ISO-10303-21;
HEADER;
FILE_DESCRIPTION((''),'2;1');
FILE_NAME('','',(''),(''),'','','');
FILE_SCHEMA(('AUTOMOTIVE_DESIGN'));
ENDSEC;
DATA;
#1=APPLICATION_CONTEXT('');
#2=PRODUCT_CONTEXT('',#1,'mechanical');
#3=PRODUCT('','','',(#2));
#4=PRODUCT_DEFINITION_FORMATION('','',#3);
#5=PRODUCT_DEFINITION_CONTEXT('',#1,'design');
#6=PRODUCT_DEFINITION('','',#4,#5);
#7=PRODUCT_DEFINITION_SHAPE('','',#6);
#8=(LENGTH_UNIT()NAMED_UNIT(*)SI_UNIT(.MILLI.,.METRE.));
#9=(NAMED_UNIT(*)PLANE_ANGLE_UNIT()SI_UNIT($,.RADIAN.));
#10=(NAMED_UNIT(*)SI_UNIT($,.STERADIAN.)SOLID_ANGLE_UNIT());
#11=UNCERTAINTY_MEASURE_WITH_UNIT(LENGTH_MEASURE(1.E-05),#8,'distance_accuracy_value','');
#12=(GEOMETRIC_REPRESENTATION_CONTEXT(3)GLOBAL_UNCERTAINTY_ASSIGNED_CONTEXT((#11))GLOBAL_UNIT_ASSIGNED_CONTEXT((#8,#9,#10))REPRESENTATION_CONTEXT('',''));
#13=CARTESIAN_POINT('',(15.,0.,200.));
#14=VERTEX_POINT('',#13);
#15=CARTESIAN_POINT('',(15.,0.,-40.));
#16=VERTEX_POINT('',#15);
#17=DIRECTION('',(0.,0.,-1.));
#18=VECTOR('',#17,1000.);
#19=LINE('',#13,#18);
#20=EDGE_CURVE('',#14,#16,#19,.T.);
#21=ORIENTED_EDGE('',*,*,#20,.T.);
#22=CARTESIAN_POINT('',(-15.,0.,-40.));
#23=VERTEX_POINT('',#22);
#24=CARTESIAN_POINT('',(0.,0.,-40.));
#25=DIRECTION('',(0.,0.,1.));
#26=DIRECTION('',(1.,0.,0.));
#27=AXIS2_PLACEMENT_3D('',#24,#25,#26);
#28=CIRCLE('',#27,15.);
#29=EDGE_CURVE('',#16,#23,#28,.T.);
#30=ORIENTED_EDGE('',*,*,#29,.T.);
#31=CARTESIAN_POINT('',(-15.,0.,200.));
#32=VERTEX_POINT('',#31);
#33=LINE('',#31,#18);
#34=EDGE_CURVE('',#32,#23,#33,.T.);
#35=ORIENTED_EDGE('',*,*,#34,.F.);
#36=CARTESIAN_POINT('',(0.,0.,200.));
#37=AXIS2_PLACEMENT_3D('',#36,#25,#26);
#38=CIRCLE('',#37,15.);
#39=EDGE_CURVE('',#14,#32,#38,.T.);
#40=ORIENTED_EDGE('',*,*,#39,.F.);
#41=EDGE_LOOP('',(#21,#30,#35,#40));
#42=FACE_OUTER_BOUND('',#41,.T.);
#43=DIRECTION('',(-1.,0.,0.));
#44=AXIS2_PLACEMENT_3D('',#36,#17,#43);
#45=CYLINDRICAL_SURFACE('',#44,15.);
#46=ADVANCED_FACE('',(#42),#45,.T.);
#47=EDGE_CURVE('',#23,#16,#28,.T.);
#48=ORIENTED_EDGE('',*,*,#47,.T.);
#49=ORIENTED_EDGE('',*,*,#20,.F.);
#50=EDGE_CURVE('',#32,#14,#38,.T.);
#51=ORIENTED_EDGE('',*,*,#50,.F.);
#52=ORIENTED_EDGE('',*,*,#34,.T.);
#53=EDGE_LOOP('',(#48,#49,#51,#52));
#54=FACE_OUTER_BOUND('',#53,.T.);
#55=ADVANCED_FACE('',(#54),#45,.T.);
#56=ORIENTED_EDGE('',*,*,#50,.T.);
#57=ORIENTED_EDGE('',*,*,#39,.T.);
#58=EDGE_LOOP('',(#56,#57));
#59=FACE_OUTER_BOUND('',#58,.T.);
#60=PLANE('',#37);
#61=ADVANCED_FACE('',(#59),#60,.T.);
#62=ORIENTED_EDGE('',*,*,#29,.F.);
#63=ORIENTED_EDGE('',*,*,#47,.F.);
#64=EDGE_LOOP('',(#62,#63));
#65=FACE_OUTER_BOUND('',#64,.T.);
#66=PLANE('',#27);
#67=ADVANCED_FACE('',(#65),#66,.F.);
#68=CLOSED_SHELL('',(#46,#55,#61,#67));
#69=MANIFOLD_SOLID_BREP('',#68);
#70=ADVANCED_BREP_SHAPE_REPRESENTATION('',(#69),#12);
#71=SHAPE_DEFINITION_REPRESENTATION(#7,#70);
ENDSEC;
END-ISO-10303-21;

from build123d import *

# Parameters (mm, degrees)
BOSS_EXTRUDE1_DEPTH      = 200
BOSS_EXTRUDE1_DEPTH_BACK = 40
SKETCH2_R                = 15


with BuildPart() as part:
    # Sketch2 → Boss-Extrude1 (new, two sides: drawn at the far end of the back side and taken through both)
    with BuildSketch(Plane.XY.offset(-BOSS_EXTRUDE1_DEPTH_BACK)):
        Circle(SKETCH2_R)
    extrude(amount=BOSS_EXTRUDE1_DEPTH + BOSS_EXTRUDE1_DEPTH_BACK)


solid = part.part
